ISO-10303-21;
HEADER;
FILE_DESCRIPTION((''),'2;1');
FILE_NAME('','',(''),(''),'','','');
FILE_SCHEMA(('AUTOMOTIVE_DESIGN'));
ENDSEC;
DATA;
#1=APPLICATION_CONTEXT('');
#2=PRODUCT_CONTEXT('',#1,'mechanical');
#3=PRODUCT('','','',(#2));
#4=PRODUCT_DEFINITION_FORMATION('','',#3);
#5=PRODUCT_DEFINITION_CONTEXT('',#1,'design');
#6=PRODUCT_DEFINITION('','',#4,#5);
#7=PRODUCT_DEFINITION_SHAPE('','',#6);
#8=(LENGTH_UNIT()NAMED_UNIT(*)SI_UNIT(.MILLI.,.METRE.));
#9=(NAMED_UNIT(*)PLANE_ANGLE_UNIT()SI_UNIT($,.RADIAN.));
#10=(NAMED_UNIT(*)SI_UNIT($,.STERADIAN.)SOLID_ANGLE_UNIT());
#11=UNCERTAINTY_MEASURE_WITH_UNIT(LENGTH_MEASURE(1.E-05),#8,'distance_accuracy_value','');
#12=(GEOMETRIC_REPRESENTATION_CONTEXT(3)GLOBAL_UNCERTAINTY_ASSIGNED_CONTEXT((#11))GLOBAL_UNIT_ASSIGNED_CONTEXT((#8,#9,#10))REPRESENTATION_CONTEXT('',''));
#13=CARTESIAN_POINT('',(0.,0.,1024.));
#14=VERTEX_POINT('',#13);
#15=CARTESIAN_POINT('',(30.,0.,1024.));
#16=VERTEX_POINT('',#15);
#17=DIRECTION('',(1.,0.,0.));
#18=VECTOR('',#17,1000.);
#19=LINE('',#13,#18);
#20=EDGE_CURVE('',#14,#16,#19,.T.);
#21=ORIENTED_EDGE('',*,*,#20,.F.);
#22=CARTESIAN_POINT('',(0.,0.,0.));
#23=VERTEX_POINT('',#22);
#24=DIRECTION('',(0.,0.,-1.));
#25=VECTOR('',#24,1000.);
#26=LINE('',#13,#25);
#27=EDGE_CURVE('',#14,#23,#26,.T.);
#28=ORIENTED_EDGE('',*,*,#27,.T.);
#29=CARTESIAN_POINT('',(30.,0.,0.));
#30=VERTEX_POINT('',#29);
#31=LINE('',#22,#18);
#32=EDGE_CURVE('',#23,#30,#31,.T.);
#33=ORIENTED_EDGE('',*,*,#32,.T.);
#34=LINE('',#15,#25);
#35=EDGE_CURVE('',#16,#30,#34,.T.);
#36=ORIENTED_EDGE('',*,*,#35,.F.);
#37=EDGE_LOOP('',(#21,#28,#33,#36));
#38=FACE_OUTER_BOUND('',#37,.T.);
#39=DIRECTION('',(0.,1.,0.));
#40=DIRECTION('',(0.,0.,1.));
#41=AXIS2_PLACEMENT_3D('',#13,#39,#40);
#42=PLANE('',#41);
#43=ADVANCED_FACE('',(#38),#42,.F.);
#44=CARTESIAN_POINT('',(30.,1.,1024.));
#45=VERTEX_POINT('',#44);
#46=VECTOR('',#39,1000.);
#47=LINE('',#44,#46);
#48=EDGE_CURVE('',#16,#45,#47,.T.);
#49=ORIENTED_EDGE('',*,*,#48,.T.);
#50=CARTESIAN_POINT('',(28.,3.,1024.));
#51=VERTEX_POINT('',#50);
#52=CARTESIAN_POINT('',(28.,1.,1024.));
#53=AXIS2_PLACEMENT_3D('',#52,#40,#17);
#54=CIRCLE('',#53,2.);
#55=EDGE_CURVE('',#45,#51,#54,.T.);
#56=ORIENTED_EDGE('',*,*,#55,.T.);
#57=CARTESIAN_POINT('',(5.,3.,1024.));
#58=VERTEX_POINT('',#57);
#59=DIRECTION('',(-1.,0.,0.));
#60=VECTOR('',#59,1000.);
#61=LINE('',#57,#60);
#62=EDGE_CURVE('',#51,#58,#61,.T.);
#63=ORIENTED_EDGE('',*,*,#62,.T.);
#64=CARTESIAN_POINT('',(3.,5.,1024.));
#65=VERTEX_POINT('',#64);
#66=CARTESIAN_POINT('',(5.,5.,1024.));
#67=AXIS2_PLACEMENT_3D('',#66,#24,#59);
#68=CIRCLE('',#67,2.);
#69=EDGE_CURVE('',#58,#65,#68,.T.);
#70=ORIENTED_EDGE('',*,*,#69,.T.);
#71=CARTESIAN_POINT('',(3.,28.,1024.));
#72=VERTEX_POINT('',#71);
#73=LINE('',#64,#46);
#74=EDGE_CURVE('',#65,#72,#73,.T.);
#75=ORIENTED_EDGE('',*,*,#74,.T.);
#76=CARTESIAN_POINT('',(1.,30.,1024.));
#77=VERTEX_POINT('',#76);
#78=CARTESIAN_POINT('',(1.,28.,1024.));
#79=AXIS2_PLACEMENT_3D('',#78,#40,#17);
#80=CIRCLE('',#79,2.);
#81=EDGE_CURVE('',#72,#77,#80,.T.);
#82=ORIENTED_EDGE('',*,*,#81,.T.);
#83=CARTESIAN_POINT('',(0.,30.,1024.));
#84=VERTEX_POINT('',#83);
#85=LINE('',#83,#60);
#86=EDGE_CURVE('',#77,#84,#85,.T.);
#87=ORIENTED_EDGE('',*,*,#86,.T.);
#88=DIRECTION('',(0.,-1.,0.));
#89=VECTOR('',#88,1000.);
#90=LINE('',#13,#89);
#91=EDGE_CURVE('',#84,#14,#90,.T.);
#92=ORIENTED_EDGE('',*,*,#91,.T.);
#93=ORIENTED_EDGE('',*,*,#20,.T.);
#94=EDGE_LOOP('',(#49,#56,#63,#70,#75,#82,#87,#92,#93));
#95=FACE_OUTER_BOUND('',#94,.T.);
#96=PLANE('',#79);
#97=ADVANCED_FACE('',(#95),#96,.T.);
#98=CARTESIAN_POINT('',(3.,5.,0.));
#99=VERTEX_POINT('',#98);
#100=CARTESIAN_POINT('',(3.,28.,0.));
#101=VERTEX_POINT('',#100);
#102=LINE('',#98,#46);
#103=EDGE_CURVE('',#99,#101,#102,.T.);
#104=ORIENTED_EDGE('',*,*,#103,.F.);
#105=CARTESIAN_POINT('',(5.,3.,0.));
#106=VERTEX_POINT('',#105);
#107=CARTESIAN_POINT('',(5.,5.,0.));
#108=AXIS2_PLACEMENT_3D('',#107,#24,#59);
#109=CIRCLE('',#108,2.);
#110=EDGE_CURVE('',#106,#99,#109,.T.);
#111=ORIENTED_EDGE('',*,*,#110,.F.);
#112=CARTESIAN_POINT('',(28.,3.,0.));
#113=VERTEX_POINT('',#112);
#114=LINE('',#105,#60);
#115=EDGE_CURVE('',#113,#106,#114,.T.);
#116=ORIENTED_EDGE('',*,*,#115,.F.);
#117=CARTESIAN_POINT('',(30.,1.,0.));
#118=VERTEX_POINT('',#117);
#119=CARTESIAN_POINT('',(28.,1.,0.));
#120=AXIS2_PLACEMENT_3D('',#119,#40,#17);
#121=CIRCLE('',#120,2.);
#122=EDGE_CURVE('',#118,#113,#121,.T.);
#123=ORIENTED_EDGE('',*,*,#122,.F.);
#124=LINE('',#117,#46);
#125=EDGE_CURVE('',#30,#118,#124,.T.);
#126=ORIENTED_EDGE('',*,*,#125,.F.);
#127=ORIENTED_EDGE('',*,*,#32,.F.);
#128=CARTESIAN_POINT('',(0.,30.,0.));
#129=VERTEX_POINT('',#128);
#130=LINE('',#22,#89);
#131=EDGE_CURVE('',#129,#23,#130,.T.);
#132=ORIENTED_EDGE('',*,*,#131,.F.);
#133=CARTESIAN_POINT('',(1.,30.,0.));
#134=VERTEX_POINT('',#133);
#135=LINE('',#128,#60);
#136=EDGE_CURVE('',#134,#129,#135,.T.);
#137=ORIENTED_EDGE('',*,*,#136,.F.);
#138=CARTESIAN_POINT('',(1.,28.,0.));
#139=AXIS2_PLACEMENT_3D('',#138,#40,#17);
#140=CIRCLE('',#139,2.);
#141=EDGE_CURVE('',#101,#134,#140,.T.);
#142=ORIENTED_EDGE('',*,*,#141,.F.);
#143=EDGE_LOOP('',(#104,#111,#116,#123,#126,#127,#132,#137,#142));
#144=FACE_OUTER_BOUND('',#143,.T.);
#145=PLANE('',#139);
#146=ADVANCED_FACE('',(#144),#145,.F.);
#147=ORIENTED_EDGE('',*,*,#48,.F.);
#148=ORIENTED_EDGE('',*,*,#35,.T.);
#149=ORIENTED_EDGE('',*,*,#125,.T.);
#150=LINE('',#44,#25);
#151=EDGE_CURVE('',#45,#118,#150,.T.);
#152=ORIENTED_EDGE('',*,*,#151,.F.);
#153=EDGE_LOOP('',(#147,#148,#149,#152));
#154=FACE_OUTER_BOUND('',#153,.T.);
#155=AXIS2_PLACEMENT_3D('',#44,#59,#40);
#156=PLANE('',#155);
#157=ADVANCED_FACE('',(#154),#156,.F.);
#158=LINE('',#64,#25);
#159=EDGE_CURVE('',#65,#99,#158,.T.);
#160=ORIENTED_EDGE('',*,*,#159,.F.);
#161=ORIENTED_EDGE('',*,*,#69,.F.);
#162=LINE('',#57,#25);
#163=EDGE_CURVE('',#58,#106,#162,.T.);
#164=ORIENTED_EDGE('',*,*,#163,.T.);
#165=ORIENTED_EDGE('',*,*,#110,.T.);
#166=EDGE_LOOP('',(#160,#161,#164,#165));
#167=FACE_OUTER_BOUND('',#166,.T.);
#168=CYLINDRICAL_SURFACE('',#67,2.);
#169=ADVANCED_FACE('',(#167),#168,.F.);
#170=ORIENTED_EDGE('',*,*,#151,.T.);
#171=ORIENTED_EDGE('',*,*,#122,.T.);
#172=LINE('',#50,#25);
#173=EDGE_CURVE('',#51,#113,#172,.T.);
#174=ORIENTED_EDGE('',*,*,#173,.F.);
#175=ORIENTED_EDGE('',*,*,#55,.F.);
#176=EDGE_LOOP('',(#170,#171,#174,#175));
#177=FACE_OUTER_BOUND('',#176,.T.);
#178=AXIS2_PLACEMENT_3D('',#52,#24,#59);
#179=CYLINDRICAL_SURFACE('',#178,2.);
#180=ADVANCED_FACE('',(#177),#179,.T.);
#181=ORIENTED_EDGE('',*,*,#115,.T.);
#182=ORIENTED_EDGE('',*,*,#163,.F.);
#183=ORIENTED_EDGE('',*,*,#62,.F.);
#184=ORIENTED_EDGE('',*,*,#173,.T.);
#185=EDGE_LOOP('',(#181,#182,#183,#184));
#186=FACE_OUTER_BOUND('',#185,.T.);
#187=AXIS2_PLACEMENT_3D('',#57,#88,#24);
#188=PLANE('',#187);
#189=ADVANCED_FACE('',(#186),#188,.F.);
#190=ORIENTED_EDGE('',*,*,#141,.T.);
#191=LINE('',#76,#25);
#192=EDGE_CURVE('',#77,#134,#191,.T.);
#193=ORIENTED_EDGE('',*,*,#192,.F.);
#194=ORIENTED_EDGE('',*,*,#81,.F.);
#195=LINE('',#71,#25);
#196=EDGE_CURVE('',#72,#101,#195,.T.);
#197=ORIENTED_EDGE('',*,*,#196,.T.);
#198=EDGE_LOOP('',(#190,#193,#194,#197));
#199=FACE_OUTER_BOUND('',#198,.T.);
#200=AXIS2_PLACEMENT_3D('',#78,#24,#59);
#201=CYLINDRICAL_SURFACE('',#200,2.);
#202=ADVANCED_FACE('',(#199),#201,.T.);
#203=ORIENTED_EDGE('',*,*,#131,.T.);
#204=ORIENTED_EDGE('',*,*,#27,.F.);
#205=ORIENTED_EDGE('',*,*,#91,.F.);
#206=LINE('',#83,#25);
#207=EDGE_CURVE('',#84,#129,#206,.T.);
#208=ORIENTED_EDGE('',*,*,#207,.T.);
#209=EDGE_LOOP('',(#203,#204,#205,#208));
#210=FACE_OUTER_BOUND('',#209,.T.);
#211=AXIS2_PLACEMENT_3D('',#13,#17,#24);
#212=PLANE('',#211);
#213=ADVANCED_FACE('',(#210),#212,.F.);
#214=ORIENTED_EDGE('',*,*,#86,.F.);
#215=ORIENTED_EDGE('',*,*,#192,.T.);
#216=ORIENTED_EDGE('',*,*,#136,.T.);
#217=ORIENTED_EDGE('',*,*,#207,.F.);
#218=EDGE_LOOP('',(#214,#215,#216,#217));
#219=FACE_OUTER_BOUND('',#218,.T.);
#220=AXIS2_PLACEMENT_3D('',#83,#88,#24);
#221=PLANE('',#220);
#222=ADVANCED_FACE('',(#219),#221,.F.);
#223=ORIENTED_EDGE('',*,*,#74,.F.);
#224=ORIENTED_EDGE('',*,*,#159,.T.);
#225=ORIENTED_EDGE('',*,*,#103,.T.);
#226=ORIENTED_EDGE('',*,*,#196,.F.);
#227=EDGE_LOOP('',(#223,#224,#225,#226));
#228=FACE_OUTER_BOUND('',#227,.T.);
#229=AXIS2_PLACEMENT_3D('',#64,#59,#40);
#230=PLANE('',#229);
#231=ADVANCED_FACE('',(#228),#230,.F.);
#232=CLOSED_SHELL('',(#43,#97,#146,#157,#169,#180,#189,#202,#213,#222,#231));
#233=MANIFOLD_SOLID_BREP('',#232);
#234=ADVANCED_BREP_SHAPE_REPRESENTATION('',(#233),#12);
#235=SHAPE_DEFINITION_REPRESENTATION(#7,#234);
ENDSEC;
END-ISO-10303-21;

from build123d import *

# Parameters (mm, degrees)
BOSS_EXTRUDE1_DEPTH = 1024


with BuildPart() as part:
    # Sketch1 → Boss-Extrude1 (new body)
    with BuildSketch(Plane.XY):
        with BuildLine():
            Line((0, 0), (30, 0))
            Line((30, 0), (30, 1))
            ThreePointArc((30, 1), (29.414213562, 2.414213562), (28, 3))
            Line((28, 3), (5, 3))
            ThreePointArc((5, 3), (3.585786438, 3.585786438), (3, 5))
            Line((3, 5), (3, 28))
            ThreePointArc((3, 28), (2.414213562, 29.414213562), (1, 30))
            Line((1, 30), (0, 30))
            Line((0, 30), (0, 0))
        make_face()
    extrude(amount=BOSS_EXTRUDE1_DEPTH)


solid = part.part
